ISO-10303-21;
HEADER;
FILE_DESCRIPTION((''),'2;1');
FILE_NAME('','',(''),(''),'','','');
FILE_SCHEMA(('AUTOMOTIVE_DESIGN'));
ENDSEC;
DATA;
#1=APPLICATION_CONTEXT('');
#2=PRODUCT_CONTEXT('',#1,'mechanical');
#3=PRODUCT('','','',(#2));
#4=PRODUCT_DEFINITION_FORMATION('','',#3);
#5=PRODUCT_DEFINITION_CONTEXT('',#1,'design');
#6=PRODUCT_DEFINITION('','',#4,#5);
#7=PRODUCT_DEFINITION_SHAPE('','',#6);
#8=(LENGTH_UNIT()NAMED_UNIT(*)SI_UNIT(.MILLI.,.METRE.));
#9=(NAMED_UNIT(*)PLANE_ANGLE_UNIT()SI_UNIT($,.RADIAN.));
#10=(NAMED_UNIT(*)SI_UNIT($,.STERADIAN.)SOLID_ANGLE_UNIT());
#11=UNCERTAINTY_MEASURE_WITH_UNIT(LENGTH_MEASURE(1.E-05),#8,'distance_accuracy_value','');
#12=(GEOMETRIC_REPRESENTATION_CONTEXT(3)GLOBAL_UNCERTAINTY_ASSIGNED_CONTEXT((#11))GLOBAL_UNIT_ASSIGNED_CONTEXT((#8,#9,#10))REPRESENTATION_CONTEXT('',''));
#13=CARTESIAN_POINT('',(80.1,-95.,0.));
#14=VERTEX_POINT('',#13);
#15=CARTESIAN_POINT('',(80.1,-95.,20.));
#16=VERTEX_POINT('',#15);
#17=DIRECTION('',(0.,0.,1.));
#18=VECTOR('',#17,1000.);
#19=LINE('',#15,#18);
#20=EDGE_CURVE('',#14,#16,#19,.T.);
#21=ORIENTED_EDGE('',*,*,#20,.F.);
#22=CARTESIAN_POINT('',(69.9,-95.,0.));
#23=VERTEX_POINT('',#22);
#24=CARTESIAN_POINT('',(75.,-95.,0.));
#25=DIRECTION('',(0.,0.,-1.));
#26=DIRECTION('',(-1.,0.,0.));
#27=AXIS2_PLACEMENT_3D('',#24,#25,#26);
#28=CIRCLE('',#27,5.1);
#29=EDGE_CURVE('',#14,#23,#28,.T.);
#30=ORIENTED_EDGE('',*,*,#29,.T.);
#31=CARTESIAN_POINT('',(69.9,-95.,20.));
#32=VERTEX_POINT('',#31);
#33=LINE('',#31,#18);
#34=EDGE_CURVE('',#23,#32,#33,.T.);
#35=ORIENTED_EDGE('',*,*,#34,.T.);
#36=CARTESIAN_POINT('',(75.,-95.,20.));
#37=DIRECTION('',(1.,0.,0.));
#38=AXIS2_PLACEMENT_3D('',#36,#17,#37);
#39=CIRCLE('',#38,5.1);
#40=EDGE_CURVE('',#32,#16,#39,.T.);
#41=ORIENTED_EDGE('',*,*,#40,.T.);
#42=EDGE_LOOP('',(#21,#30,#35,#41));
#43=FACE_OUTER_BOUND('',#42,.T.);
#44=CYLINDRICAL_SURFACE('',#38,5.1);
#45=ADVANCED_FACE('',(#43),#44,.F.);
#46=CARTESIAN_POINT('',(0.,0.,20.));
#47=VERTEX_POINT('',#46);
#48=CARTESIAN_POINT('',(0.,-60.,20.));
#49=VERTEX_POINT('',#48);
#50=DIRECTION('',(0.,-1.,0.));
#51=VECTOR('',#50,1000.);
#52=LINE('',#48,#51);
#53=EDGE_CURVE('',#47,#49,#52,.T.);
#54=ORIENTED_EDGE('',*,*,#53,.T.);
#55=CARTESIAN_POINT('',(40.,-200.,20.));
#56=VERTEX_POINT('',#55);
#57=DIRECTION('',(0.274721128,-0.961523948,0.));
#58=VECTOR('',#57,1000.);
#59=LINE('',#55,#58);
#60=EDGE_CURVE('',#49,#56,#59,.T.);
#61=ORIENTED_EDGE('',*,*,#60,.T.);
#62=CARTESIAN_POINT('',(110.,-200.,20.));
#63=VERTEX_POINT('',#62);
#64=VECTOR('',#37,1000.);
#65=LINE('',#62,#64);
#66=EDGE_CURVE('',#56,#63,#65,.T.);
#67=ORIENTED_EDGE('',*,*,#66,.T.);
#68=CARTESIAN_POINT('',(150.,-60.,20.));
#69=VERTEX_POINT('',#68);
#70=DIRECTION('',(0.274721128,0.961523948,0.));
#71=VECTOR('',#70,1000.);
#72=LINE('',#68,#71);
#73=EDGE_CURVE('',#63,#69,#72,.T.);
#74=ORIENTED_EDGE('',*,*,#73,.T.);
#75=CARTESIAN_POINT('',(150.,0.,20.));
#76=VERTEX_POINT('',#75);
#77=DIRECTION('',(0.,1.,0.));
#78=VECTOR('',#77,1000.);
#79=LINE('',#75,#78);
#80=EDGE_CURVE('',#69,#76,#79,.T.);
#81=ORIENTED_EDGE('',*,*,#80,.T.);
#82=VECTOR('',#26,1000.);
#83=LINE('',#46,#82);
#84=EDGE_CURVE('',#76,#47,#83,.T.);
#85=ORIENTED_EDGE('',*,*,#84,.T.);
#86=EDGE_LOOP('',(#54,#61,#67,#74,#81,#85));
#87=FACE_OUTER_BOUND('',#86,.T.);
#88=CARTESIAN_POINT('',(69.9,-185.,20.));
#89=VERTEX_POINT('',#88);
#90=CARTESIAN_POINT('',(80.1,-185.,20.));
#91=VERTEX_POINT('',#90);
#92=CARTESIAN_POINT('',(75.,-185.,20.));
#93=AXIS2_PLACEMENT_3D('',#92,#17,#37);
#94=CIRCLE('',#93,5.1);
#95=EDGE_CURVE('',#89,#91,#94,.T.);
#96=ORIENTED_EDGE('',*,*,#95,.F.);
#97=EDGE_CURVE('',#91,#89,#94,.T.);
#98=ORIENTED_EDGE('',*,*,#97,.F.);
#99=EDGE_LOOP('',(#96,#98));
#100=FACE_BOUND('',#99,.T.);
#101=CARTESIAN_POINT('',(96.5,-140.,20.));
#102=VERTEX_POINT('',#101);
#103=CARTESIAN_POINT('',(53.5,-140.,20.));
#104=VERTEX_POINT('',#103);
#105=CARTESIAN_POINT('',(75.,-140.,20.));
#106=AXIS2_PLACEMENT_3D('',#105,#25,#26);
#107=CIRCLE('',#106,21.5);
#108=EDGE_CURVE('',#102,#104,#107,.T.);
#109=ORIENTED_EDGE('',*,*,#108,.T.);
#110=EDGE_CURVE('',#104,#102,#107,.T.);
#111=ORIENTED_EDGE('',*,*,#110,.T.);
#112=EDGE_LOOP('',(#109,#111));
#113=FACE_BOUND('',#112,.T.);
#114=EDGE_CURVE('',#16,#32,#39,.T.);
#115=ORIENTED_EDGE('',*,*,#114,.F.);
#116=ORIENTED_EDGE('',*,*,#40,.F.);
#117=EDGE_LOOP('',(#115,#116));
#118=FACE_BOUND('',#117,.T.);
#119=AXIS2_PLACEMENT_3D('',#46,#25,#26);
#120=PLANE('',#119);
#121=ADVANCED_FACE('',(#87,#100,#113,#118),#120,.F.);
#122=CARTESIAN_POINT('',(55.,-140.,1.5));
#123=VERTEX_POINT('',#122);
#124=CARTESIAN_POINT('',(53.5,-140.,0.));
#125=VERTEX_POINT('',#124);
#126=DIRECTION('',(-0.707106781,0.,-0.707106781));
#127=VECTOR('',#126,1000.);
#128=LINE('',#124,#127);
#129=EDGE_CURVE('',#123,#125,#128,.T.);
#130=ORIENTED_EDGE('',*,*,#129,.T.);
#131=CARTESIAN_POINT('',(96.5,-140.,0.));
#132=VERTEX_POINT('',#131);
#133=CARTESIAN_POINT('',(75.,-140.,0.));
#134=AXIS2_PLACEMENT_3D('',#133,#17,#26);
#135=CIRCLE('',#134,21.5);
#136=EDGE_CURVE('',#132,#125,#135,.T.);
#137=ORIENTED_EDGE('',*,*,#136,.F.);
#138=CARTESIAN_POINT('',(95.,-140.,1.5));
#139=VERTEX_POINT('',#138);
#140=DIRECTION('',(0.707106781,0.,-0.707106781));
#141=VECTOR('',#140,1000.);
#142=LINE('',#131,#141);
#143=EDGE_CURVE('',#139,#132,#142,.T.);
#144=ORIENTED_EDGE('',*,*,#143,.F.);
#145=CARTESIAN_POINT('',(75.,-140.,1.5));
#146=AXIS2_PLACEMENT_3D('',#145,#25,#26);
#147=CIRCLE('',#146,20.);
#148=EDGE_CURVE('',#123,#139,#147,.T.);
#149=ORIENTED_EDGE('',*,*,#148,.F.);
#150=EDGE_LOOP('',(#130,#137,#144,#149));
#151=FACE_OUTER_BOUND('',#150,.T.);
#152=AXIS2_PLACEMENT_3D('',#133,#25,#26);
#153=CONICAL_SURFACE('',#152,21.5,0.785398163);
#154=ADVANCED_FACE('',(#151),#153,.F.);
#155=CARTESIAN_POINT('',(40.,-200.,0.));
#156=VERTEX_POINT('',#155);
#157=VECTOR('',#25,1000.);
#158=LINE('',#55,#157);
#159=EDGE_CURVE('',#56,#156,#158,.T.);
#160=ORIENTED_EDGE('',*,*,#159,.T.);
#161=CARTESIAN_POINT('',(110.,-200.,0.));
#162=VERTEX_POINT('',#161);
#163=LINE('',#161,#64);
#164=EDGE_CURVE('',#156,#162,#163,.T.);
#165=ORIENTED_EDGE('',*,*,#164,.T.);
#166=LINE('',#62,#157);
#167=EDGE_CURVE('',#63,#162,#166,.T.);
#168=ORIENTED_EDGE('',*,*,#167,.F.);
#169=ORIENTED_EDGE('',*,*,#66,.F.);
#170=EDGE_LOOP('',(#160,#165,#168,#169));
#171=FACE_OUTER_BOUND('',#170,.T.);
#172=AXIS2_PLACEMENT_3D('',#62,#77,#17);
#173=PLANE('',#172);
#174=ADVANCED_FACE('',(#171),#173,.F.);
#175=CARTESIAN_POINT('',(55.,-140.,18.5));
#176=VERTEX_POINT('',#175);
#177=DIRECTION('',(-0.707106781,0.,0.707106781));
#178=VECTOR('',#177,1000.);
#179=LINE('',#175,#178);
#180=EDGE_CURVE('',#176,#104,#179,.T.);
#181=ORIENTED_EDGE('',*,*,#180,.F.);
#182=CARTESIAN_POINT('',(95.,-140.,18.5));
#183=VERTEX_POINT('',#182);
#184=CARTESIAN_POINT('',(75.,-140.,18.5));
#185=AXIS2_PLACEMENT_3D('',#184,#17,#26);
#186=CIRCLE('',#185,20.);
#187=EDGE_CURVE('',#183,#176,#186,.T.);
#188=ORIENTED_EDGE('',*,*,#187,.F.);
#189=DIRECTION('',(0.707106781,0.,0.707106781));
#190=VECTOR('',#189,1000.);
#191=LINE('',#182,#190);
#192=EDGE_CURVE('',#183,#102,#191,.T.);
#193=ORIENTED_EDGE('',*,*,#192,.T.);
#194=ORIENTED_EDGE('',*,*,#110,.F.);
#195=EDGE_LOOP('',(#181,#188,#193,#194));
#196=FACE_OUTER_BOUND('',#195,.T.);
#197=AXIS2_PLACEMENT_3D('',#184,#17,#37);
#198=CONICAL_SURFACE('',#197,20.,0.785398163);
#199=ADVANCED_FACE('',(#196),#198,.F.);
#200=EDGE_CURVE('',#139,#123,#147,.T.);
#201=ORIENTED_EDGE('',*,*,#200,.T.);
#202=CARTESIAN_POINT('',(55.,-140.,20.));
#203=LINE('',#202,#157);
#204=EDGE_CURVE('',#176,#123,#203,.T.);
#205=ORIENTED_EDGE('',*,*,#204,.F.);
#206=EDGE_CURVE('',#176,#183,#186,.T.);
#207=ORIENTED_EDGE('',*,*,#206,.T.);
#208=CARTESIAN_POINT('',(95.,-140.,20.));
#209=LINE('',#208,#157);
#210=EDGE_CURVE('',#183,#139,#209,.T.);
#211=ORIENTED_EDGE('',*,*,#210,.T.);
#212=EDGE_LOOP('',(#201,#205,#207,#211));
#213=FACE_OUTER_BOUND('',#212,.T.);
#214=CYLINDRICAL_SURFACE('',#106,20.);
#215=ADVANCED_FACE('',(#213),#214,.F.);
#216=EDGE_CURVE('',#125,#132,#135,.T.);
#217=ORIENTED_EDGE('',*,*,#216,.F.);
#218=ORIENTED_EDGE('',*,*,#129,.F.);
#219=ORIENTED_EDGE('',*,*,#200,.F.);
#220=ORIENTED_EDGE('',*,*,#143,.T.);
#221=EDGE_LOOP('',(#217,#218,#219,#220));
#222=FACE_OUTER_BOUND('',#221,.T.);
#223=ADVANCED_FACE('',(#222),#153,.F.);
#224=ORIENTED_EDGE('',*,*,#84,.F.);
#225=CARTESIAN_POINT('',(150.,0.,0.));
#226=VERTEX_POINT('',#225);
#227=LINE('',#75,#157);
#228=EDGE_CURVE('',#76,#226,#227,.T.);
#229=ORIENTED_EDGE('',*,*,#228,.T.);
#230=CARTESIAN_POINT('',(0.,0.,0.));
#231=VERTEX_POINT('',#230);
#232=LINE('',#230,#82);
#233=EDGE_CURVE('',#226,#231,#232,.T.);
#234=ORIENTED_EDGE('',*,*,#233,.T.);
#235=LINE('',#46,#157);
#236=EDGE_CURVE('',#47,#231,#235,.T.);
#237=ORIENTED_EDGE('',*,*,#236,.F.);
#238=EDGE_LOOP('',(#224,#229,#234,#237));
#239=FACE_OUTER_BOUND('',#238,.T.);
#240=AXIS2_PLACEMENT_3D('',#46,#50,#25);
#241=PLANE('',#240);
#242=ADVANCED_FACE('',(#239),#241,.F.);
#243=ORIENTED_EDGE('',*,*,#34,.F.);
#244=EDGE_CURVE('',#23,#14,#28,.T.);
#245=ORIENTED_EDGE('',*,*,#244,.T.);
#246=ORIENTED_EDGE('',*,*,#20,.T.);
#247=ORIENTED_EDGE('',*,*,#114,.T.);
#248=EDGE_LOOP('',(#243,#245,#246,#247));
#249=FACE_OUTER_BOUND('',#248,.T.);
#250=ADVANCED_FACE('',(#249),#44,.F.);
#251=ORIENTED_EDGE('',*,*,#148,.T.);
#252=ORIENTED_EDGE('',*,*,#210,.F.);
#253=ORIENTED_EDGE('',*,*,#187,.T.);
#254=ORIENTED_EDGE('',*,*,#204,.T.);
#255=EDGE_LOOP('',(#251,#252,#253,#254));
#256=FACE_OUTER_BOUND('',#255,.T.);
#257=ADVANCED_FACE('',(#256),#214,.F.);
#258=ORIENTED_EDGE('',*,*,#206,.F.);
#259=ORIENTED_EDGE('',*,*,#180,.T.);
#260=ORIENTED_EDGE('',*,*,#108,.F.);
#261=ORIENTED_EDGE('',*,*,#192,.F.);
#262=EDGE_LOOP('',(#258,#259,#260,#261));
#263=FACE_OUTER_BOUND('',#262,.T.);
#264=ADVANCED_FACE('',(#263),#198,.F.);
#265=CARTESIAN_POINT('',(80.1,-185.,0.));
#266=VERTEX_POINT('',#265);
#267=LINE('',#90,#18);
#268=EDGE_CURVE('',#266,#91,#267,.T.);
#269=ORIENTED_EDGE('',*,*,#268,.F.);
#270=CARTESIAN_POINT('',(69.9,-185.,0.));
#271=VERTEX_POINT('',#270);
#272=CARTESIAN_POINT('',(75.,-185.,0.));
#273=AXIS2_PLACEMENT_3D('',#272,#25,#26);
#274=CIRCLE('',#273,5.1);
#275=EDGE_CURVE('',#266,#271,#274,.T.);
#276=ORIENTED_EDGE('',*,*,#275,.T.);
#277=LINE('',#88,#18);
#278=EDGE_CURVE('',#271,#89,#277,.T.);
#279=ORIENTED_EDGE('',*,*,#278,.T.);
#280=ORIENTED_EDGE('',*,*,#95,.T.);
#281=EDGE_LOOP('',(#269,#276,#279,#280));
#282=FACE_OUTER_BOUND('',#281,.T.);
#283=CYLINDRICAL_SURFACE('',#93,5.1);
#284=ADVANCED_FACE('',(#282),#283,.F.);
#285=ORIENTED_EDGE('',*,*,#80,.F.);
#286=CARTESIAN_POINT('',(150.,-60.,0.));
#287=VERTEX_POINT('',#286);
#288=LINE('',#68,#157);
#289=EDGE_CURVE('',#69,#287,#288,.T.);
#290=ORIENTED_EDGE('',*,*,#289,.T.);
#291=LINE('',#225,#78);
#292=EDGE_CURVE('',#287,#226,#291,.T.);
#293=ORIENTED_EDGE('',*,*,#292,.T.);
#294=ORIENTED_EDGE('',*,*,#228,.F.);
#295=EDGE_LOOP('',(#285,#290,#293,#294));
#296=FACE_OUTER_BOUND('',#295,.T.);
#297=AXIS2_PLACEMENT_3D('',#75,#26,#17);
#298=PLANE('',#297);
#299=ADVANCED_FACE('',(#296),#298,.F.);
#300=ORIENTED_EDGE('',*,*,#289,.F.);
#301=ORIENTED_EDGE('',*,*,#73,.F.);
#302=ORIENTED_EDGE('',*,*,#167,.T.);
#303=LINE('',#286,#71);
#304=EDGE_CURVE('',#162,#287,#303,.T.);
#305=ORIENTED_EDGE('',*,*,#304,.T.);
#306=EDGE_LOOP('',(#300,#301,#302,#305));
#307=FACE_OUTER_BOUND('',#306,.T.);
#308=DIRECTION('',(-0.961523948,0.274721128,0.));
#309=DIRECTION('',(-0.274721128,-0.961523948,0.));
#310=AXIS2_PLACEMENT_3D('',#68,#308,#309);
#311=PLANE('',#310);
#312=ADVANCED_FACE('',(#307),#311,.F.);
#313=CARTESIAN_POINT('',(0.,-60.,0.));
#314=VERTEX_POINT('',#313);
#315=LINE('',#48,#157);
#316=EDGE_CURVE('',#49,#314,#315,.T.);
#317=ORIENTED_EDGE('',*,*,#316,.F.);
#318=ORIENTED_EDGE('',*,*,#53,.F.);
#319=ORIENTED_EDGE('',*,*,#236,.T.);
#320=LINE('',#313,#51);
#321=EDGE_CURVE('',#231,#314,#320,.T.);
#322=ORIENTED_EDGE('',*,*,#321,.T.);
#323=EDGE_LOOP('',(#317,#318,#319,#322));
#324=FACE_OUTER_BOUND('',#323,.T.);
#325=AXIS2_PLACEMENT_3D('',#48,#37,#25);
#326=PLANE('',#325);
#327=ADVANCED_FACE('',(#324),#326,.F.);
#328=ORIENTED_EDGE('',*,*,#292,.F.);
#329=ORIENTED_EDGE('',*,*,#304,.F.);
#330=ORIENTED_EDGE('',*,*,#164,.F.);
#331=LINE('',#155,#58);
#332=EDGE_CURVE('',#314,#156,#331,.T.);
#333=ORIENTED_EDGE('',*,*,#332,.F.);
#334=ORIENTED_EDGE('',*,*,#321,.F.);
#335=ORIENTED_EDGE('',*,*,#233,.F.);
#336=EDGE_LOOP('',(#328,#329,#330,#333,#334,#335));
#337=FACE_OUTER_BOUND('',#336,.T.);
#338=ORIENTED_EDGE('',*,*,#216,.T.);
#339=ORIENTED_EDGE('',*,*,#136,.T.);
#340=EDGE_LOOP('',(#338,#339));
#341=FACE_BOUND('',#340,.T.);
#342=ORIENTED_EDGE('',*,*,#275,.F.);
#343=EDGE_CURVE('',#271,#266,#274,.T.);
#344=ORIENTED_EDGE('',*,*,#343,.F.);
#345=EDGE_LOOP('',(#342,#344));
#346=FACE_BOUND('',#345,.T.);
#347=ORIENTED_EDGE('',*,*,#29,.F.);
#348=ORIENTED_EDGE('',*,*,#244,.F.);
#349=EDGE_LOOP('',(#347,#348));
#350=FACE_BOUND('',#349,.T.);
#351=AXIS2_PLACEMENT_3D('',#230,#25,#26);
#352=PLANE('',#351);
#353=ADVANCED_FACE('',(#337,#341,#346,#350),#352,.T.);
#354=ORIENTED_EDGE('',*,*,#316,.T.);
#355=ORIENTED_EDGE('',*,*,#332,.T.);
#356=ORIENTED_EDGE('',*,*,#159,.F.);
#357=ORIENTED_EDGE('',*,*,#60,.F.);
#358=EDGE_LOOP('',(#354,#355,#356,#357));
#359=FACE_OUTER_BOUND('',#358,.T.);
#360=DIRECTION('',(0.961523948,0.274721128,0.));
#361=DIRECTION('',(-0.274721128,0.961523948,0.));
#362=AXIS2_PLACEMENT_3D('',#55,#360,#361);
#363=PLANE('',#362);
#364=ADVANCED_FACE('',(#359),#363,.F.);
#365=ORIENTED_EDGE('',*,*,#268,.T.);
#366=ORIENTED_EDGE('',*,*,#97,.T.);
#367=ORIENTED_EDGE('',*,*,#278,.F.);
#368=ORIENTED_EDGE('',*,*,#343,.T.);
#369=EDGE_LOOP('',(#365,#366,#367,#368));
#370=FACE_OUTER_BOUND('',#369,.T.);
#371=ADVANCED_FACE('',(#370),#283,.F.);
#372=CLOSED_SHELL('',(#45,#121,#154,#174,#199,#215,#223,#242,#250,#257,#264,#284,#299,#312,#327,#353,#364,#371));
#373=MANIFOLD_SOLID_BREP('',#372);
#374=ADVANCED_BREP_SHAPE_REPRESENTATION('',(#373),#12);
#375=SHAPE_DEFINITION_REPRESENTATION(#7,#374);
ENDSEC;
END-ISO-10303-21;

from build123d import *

# Parameters (mm, degrees)
SKETCH1_R              = 20
BOSS_EXTRUDE1_DEPTH    = 20
M12_TAPPED_HOLE1_D     = 10.2
M12_TAPPED_HOLE1_DEPTH = 29.25
M12_TAPPED_HOLE1_TIP   = 3.064389157
CHAMFER1_SIZE          = 1.5


with BuildPart() as part:
    # Sketch1 → Boss-Extrude1 (new body)
    with BuildSketch(Plane.XY):
        Polygon((0, 0), (150, 0), (150, -60), (110, -200), (40, -200), (0, -60), align=None)
        with Locations((75, -140)):
            Circle(SKETCH1_R, mode=Mode.SUBTRACT)
    extrude(amount=BOSS_EXTRUDE1_DEPTH)

    # M12 Tapped Hole1
    with Locations(Plane.XY.offset(20)):
        with Locations((75, -95), (75, -185)):
            Hole(M12_TAPPED_HOLE1_D / 2, depth=M12_TAPPED_HOLE1_DEPTH)
            with Locations((0, 0, -(M12_TAPPED_HOLE1_DEPTH + M12_TAPPED_HOLE1_TIP / 2))):  # 118° drill point
                Cone(0, M12_TAPPED_HOLE1_D / 2, M12_TAPPED_HOLE1_TIP, mode=Mode.SUBTRACT)

    # Chamfer1
    chamfer1_edges = [part.edges().sort_by_distance(p)[0] for p in [
        (55, -140, 0),
        (55, -140, 20),
    ]]
    chamfer(chamfer1_edges, length=CHAMFER1_SIZE)


solid = part.part
